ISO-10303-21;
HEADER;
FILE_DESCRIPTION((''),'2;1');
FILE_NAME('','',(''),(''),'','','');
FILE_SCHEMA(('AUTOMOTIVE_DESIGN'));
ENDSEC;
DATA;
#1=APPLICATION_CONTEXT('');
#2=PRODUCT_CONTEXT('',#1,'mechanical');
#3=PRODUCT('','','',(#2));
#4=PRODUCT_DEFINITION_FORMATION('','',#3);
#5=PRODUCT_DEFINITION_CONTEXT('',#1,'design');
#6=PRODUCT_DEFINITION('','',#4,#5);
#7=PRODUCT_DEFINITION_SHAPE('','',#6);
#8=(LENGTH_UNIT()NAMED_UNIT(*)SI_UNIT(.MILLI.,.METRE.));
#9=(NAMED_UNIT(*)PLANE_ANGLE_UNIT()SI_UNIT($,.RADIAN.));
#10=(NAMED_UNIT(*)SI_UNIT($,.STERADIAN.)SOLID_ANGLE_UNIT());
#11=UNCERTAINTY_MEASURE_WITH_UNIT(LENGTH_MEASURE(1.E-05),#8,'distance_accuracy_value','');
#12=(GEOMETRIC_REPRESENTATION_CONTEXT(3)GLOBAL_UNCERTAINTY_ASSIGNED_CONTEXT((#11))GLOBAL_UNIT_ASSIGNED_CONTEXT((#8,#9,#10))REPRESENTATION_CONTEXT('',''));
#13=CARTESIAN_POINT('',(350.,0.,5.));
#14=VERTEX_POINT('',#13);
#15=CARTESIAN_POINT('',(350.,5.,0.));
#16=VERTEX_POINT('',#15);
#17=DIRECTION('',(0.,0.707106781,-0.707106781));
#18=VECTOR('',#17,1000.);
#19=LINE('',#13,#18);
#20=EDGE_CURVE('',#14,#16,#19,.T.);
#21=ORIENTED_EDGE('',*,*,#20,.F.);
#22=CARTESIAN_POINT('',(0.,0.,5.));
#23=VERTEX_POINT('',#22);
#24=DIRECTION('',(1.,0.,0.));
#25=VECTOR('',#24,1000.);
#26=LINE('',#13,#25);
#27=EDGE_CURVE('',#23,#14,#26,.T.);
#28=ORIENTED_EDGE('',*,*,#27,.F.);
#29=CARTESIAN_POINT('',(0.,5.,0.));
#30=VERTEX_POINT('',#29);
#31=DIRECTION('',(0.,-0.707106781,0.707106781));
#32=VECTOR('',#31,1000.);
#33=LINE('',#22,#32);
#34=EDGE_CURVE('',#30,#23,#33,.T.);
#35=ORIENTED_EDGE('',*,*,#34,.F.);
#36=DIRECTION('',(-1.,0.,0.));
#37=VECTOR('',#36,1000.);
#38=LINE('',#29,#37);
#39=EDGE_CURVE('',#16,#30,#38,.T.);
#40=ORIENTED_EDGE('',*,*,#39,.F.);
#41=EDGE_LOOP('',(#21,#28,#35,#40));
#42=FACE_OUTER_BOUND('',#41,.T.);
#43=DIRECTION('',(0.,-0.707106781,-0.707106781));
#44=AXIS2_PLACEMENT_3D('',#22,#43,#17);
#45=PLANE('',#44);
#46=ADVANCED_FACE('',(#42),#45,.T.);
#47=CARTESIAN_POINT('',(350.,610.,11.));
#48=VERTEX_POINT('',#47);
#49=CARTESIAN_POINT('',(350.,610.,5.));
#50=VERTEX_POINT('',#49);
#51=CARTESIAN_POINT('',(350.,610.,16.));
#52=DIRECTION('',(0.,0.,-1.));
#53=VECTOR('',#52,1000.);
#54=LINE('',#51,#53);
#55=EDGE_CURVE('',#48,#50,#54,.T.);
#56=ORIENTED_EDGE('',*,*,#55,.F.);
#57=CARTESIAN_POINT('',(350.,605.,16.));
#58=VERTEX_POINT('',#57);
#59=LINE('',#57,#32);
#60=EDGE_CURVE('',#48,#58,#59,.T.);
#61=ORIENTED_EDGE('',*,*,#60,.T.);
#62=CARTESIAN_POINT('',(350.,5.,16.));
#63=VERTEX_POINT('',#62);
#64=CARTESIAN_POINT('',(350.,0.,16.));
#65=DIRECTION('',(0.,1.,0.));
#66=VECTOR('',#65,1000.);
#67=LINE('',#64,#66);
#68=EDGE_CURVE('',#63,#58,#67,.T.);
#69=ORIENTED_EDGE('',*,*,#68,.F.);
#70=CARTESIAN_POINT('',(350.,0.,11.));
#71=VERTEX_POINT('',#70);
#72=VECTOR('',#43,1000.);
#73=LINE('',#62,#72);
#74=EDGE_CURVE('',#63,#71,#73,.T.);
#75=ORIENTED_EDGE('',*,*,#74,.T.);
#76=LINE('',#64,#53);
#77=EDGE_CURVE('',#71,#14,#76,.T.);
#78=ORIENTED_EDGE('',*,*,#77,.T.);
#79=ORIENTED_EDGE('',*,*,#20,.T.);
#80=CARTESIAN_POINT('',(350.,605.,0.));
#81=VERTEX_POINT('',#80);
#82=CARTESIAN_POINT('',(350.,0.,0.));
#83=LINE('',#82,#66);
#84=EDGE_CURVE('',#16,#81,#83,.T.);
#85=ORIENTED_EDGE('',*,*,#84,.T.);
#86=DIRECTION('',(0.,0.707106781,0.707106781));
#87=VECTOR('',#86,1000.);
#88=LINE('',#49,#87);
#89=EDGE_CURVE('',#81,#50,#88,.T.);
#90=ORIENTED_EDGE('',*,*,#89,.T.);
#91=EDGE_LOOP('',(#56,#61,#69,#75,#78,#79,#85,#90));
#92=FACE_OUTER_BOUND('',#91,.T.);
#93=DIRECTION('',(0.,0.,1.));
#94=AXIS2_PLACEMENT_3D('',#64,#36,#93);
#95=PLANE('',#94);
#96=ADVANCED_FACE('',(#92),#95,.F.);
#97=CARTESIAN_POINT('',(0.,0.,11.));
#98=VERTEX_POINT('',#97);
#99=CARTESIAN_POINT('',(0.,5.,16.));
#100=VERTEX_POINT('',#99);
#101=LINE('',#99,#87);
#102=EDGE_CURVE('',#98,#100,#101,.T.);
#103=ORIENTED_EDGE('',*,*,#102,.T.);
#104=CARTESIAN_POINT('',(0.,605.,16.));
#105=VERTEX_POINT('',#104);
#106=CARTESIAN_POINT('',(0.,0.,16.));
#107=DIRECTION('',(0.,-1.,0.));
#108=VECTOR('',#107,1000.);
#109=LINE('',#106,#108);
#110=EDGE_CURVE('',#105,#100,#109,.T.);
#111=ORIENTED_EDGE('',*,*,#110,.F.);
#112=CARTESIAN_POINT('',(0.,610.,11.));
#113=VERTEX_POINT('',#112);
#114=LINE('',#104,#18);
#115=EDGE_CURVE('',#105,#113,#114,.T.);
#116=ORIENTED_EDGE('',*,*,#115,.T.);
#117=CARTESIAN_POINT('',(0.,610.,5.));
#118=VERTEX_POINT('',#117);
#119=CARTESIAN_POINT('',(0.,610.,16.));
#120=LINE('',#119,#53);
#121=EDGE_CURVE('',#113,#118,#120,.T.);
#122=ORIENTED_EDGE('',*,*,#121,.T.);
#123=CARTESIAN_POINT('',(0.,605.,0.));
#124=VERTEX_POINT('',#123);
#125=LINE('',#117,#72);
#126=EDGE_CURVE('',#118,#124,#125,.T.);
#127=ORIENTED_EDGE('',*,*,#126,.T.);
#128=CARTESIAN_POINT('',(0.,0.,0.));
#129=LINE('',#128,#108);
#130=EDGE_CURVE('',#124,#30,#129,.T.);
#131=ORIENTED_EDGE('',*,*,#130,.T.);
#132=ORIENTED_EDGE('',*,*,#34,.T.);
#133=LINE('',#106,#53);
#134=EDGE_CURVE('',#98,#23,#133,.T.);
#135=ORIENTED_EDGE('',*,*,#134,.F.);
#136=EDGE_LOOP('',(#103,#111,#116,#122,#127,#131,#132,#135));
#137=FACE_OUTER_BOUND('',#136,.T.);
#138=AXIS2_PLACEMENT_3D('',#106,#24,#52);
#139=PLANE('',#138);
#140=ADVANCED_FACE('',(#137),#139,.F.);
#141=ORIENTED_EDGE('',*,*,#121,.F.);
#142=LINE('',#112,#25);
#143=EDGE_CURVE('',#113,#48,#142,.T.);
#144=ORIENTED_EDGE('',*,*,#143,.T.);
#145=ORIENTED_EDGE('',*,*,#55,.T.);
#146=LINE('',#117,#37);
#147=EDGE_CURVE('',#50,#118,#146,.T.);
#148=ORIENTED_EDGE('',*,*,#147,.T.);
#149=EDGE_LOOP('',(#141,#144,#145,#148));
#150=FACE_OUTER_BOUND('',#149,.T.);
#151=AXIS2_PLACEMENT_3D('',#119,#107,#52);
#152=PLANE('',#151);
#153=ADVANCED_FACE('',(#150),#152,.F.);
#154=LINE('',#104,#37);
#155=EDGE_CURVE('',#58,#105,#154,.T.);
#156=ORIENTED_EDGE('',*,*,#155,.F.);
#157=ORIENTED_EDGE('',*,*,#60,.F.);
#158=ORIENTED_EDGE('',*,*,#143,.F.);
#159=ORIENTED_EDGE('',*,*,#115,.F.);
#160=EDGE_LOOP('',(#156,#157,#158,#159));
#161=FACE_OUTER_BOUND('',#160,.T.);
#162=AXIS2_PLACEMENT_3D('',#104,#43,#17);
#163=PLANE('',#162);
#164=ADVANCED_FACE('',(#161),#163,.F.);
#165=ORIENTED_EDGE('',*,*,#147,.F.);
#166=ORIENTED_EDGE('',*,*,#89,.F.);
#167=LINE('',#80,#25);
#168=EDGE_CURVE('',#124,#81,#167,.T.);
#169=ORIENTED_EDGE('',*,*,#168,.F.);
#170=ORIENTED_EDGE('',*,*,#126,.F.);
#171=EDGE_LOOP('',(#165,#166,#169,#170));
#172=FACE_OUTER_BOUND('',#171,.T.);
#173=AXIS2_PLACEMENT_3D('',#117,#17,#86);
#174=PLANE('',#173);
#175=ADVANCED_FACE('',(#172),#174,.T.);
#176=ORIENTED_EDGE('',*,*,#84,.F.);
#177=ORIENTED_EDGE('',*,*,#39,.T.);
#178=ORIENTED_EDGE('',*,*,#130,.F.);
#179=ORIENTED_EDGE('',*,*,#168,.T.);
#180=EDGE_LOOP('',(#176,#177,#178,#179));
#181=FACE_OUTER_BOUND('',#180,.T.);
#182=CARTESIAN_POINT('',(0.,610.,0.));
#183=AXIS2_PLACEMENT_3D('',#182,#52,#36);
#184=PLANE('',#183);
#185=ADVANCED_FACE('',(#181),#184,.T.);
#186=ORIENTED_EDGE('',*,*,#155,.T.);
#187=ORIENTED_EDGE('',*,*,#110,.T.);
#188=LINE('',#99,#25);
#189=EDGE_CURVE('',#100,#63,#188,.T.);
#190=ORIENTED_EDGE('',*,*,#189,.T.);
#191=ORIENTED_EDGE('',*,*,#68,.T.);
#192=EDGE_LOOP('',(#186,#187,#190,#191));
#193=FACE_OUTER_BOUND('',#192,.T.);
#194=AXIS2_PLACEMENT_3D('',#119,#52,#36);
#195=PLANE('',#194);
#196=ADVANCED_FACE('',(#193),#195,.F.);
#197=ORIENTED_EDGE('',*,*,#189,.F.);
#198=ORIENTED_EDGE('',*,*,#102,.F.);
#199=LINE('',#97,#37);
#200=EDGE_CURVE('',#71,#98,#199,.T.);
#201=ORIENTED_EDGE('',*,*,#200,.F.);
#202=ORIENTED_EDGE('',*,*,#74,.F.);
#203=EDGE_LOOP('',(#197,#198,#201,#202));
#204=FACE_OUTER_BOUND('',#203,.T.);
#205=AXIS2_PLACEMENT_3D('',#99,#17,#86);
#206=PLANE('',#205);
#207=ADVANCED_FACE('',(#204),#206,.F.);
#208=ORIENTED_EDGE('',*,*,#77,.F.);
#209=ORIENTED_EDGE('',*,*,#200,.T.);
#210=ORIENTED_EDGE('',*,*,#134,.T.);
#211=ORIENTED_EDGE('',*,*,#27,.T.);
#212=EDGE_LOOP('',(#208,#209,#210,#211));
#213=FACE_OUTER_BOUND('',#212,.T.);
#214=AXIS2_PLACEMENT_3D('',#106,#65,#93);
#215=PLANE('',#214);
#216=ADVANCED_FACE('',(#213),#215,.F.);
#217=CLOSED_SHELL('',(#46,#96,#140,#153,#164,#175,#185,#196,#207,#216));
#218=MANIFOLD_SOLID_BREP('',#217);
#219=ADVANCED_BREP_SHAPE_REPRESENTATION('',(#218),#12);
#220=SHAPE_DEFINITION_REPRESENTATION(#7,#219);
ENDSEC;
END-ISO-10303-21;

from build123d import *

# Parameters (mm, degrees)
SKETCH1_W           = 350
SKETCH1_H           = 610
BOSS_EXTRUDE1_DEPTH = 16
CHAMFER1_SIZE       = 5


with BuildPart() as part:
    # Sketch1 → Boss-Extrude1 (new body)
    with BuildSketch(Plane.XY):
        with Locations((175, 305)):
            Rectangle(SKETCH1_W, SKETCH1_H)
    extrude(amount=BOSS_EXTRUDE1_DEPTH)

    # Chamfer1
    chamfer1_edges = [part.edges().sort_by_distance(p)[0] for p in [
        (175, 610, 16),
        (175, 610, 0),
        (175, 0, 0),
        (175, 0, 16),
    ]]
    chamfer(chamfer1_edges, length=CHAMFER1_SIZE)


solid = part.part
